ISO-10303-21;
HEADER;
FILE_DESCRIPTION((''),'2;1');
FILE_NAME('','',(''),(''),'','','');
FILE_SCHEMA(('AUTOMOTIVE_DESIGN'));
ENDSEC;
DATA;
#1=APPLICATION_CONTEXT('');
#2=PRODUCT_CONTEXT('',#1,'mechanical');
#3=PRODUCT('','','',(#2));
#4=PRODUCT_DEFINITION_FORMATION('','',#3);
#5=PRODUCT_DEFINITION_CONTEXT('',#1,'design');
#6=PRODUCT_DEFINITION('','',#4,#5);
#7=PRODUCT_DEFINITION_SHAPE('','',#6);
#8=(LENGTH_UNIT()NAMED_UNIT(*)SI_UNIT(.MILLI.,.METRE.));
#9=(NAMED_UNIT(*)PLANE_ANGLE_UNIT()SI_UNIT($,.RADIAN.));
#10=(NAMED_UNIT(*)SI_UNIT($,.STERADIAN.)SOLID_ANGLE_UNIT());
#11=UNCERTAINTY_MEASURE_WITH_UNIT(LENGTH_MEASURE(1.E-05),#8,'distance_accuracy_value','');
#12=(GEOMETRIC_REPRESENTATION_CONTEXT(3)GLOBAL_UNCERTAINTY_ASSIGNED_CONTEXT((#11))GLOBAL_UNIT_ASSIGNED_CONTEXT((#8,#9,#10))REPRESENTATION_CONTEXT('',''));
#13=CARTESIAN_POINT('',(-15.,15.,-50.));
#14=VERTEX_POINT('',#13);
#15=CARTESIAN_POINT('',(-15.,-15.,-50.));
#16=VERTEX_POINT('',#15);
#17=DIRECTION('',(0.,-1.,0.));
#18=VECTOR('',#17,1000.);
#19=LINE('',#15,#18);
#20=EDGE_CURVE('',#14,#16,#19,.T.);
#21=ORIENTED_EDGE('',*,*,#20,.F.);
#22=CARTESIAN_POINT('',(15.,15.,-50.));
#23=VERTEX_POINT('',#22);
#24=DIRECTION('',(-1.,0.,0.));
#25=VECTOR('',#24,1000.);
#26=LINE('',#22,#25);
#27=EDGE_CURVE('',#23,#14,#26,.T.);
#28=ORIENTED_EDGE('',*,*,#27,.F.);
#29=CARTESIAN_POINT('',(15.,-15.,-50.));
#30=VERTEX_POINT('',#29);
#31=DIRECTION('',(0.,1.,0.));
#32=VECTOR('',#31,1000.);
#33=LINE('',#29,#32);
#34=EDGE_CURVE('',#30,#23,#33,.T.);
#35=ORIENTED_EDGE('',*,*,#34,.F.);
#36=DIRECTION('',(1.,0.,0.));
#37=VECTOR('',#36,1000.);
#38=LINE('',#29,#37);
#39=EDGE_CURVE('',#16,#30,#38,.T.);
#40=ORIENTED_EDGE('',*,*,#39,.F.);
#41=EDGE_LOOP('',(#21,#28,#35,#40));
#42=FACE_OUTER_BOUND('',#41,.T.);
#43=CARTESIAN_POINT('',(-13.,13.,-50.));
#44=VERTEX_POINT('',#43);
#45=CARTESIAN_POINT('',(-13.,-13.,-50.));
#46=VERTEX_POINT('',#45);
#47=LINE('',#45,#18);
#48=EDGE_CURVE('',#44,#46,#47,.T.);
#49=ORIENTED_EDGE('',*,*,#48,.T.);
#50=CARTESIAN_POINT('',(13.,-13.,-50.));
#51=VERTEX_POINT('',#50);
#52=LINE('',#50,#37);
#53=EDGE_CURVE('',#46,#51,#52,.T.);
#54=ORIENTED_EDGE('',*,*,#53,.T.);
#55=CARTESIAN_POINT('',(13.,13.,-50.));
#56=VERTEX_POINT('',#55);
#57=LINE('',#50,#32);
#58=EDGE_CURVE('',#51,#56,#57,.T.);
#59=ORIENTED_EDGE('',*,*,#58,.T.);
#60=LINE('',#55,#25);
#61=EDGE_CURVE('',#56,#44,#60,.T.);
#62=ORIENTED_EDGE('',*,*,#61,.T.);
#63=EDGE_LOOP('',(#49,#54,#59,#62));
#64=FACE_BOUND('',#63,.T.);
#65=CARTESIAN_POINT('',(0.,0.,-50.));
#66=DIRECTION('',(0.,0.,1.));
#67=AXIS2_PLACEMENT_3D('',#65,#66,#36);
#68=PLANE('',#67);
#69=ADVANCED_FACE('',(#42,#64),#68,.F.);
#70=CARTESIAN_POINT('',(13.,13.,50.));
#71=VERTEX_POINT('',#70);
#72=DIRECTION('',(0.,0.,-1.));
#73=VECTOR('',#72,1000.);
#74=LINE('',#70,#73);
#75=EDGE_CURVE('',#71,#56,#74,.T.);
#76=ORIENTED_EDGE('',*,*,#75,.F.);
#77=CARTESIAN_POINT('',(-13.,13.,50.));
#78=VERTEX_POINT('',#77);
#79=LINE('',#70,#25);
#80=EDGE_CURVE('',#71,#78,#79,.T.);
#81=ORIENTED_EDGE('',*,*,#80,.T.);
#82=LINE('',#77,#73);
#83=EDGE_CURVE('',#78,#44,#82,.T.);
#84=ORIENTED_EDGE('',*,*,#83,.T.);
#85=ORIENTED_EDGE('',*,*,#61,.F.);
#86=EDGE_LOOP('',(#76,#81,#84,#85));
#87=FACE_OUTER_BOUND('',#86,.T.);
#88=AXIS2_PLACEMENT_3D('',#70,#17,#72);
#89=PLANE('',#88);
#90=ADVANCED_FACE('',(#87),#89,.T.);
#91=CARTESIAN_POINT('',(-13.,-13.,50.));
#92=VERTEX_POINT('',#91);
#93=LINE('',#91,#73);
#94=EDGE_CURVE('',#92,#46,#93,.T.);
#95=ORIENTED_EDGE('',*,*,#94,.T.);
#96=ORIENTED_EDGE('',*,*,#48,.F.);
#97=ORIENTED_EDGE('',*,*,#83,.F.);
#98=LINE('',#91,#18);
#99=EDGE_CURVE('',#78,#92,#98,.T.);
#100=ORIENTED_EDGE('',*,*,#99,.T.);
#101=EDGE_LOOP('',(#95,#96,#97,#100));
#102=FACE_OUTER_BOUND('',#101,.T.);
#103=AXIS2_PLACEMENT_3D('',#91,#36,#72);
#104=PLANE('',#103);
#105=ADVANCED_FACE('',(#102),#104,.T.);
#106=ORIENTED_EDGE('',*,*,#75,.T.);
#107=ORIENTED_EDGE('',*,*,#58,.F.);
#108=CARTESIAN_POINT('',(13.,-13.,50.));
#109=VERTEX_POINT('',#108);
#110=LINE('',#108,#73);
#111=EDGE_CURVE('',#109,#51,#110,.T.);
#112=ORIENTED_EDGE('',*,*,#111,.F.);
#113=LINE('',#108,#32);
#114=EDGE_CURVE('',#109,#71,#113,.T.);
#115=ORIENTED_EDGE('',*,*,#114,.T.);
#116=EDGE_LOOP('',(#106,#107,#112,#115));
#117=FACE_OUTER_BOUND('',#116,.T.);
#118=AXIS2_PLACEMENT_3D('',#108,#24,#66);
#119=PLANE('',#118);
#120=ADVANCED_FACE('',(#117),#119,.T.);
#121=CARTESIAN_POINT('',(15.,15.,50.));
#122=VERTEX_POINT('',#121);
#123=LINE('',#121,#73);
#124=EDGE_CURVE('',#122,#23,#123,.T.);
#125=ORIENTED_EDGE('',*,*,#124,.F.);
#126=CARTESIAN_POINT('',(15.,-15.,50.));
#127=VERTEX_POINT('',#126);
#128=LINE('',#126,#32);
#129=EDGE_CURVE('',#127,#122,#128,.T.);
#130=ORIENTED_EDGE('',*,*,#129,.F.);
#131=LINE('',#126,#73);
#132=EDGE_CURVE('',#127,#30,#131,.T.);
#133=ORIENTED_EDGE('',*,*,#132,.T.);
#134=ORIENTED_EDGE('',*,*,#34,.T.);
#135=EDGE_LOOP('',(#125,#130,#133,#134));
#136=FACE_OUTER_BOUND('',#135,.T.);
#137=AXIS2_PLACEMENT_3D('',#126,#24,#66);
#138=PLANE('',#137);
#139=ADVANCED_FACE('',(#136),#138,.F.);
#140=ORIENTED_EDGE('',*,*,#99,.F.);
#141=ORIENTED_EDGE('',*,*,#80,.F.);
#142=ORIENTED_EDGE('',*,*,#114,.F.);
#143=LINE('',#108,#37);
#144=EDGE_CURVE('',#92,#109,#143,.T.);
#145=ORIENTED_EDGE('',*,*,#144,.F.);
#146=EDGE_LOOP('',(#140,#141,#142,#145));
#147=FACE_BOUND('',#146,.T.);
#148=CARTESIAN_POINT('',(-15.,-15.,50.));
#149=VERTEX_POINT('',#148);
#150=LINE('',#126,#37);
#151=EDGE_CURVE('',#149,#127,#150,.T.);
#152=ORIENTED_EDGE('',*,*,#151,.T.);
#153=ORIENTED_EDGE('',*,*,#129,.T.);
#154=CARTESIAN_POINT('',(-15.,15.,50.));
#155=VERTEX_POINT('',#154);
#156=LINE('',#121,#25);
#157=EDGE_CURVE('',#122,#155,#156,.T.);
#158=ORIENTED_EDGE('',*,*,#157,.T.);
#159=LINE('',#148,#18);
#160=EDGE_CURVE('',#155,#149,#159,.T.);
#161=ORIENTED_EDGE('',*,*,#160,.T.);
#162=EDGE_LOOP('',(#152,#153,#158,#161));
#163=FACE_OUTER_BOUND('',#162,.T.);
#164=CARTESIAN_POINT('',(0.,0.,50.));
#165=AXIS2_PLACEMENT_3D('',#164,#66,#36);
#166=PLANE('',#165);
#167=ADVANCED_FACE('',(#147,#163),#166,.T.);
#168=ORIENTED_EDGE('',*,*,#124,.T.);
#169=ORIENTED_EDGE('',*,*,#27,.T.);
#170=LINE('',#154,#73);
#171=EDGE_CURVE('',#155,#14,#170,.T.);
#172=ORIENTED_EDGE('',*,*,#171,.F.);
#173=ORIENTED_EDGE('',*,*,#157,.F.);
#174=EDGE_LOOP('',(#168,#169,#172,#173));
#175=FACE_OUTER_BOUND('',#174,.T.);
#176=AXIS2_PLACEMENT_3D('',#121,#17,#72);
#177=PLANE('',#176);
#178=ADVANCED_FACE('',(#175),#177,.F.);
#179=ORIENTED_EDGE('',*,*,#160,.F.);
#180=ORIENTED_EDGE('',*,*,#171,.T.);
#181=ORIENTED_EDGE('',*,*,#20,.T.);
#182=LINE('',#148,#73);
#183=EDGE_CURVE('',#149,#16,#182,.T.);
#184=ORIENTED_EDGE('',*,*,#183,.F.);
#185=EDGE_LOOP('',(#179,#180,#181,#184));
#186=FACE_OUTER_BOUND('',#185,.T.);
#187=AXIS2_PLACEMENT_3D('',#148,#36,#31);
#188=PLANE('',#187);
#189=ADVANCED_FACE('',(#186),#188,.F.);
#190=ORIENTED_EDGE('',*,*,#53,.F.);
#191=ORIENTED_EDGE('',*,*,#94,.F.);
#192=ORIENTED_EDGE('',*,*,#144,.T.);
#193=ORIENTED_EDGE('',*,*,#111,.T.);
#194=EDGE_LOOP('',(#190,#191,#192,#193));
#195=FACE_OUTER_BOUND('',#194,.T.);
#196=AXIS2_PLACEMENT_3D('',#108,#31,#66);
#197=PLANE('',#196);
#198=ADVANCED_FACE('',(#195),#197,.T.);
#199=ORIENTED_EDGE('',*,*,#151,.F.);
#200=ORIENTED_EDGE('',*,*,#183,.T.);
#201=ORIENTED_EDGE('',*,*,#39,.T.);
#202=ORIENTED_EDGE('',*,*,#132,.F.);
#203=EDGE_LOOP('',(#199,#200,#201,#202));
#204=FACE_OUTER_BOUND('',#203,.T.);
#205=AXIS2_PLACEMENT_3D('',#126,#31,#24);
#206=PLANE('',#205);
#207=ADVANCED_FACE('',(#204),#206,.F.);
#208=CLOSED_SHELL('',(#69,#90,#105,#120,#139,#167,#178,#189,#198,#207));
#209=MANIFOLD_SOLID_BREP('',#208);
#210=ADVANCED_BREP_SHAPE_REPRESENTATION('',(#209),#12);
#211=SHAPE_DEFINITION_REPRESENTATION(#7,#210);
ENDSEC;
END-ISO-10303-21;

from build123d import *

# Parameters (mm, degrees)
SKETCH_1_W      = 30
SKETCH_1_H      = 30
SKETCH_1_W_2    = 26
SKETCH_1_H_2    = 26
EXTRUDE_1_DEPTH = 50


with BuildPart() as part:
    # 草图1 → 凸台-拉伸1 (new, symmetric)
    with BuildSketch(Plane.XY):
        Rectangle(SKETCH_1_W, SKETCH_1_H)
        Rectangle(SKETCH_1_W_2, SKETCH_1_H_2, mode=Mode.SUBTRACT)
    extrude(amount=EXTRUDE_1_DEPTH, both=True)


solid = part.part
